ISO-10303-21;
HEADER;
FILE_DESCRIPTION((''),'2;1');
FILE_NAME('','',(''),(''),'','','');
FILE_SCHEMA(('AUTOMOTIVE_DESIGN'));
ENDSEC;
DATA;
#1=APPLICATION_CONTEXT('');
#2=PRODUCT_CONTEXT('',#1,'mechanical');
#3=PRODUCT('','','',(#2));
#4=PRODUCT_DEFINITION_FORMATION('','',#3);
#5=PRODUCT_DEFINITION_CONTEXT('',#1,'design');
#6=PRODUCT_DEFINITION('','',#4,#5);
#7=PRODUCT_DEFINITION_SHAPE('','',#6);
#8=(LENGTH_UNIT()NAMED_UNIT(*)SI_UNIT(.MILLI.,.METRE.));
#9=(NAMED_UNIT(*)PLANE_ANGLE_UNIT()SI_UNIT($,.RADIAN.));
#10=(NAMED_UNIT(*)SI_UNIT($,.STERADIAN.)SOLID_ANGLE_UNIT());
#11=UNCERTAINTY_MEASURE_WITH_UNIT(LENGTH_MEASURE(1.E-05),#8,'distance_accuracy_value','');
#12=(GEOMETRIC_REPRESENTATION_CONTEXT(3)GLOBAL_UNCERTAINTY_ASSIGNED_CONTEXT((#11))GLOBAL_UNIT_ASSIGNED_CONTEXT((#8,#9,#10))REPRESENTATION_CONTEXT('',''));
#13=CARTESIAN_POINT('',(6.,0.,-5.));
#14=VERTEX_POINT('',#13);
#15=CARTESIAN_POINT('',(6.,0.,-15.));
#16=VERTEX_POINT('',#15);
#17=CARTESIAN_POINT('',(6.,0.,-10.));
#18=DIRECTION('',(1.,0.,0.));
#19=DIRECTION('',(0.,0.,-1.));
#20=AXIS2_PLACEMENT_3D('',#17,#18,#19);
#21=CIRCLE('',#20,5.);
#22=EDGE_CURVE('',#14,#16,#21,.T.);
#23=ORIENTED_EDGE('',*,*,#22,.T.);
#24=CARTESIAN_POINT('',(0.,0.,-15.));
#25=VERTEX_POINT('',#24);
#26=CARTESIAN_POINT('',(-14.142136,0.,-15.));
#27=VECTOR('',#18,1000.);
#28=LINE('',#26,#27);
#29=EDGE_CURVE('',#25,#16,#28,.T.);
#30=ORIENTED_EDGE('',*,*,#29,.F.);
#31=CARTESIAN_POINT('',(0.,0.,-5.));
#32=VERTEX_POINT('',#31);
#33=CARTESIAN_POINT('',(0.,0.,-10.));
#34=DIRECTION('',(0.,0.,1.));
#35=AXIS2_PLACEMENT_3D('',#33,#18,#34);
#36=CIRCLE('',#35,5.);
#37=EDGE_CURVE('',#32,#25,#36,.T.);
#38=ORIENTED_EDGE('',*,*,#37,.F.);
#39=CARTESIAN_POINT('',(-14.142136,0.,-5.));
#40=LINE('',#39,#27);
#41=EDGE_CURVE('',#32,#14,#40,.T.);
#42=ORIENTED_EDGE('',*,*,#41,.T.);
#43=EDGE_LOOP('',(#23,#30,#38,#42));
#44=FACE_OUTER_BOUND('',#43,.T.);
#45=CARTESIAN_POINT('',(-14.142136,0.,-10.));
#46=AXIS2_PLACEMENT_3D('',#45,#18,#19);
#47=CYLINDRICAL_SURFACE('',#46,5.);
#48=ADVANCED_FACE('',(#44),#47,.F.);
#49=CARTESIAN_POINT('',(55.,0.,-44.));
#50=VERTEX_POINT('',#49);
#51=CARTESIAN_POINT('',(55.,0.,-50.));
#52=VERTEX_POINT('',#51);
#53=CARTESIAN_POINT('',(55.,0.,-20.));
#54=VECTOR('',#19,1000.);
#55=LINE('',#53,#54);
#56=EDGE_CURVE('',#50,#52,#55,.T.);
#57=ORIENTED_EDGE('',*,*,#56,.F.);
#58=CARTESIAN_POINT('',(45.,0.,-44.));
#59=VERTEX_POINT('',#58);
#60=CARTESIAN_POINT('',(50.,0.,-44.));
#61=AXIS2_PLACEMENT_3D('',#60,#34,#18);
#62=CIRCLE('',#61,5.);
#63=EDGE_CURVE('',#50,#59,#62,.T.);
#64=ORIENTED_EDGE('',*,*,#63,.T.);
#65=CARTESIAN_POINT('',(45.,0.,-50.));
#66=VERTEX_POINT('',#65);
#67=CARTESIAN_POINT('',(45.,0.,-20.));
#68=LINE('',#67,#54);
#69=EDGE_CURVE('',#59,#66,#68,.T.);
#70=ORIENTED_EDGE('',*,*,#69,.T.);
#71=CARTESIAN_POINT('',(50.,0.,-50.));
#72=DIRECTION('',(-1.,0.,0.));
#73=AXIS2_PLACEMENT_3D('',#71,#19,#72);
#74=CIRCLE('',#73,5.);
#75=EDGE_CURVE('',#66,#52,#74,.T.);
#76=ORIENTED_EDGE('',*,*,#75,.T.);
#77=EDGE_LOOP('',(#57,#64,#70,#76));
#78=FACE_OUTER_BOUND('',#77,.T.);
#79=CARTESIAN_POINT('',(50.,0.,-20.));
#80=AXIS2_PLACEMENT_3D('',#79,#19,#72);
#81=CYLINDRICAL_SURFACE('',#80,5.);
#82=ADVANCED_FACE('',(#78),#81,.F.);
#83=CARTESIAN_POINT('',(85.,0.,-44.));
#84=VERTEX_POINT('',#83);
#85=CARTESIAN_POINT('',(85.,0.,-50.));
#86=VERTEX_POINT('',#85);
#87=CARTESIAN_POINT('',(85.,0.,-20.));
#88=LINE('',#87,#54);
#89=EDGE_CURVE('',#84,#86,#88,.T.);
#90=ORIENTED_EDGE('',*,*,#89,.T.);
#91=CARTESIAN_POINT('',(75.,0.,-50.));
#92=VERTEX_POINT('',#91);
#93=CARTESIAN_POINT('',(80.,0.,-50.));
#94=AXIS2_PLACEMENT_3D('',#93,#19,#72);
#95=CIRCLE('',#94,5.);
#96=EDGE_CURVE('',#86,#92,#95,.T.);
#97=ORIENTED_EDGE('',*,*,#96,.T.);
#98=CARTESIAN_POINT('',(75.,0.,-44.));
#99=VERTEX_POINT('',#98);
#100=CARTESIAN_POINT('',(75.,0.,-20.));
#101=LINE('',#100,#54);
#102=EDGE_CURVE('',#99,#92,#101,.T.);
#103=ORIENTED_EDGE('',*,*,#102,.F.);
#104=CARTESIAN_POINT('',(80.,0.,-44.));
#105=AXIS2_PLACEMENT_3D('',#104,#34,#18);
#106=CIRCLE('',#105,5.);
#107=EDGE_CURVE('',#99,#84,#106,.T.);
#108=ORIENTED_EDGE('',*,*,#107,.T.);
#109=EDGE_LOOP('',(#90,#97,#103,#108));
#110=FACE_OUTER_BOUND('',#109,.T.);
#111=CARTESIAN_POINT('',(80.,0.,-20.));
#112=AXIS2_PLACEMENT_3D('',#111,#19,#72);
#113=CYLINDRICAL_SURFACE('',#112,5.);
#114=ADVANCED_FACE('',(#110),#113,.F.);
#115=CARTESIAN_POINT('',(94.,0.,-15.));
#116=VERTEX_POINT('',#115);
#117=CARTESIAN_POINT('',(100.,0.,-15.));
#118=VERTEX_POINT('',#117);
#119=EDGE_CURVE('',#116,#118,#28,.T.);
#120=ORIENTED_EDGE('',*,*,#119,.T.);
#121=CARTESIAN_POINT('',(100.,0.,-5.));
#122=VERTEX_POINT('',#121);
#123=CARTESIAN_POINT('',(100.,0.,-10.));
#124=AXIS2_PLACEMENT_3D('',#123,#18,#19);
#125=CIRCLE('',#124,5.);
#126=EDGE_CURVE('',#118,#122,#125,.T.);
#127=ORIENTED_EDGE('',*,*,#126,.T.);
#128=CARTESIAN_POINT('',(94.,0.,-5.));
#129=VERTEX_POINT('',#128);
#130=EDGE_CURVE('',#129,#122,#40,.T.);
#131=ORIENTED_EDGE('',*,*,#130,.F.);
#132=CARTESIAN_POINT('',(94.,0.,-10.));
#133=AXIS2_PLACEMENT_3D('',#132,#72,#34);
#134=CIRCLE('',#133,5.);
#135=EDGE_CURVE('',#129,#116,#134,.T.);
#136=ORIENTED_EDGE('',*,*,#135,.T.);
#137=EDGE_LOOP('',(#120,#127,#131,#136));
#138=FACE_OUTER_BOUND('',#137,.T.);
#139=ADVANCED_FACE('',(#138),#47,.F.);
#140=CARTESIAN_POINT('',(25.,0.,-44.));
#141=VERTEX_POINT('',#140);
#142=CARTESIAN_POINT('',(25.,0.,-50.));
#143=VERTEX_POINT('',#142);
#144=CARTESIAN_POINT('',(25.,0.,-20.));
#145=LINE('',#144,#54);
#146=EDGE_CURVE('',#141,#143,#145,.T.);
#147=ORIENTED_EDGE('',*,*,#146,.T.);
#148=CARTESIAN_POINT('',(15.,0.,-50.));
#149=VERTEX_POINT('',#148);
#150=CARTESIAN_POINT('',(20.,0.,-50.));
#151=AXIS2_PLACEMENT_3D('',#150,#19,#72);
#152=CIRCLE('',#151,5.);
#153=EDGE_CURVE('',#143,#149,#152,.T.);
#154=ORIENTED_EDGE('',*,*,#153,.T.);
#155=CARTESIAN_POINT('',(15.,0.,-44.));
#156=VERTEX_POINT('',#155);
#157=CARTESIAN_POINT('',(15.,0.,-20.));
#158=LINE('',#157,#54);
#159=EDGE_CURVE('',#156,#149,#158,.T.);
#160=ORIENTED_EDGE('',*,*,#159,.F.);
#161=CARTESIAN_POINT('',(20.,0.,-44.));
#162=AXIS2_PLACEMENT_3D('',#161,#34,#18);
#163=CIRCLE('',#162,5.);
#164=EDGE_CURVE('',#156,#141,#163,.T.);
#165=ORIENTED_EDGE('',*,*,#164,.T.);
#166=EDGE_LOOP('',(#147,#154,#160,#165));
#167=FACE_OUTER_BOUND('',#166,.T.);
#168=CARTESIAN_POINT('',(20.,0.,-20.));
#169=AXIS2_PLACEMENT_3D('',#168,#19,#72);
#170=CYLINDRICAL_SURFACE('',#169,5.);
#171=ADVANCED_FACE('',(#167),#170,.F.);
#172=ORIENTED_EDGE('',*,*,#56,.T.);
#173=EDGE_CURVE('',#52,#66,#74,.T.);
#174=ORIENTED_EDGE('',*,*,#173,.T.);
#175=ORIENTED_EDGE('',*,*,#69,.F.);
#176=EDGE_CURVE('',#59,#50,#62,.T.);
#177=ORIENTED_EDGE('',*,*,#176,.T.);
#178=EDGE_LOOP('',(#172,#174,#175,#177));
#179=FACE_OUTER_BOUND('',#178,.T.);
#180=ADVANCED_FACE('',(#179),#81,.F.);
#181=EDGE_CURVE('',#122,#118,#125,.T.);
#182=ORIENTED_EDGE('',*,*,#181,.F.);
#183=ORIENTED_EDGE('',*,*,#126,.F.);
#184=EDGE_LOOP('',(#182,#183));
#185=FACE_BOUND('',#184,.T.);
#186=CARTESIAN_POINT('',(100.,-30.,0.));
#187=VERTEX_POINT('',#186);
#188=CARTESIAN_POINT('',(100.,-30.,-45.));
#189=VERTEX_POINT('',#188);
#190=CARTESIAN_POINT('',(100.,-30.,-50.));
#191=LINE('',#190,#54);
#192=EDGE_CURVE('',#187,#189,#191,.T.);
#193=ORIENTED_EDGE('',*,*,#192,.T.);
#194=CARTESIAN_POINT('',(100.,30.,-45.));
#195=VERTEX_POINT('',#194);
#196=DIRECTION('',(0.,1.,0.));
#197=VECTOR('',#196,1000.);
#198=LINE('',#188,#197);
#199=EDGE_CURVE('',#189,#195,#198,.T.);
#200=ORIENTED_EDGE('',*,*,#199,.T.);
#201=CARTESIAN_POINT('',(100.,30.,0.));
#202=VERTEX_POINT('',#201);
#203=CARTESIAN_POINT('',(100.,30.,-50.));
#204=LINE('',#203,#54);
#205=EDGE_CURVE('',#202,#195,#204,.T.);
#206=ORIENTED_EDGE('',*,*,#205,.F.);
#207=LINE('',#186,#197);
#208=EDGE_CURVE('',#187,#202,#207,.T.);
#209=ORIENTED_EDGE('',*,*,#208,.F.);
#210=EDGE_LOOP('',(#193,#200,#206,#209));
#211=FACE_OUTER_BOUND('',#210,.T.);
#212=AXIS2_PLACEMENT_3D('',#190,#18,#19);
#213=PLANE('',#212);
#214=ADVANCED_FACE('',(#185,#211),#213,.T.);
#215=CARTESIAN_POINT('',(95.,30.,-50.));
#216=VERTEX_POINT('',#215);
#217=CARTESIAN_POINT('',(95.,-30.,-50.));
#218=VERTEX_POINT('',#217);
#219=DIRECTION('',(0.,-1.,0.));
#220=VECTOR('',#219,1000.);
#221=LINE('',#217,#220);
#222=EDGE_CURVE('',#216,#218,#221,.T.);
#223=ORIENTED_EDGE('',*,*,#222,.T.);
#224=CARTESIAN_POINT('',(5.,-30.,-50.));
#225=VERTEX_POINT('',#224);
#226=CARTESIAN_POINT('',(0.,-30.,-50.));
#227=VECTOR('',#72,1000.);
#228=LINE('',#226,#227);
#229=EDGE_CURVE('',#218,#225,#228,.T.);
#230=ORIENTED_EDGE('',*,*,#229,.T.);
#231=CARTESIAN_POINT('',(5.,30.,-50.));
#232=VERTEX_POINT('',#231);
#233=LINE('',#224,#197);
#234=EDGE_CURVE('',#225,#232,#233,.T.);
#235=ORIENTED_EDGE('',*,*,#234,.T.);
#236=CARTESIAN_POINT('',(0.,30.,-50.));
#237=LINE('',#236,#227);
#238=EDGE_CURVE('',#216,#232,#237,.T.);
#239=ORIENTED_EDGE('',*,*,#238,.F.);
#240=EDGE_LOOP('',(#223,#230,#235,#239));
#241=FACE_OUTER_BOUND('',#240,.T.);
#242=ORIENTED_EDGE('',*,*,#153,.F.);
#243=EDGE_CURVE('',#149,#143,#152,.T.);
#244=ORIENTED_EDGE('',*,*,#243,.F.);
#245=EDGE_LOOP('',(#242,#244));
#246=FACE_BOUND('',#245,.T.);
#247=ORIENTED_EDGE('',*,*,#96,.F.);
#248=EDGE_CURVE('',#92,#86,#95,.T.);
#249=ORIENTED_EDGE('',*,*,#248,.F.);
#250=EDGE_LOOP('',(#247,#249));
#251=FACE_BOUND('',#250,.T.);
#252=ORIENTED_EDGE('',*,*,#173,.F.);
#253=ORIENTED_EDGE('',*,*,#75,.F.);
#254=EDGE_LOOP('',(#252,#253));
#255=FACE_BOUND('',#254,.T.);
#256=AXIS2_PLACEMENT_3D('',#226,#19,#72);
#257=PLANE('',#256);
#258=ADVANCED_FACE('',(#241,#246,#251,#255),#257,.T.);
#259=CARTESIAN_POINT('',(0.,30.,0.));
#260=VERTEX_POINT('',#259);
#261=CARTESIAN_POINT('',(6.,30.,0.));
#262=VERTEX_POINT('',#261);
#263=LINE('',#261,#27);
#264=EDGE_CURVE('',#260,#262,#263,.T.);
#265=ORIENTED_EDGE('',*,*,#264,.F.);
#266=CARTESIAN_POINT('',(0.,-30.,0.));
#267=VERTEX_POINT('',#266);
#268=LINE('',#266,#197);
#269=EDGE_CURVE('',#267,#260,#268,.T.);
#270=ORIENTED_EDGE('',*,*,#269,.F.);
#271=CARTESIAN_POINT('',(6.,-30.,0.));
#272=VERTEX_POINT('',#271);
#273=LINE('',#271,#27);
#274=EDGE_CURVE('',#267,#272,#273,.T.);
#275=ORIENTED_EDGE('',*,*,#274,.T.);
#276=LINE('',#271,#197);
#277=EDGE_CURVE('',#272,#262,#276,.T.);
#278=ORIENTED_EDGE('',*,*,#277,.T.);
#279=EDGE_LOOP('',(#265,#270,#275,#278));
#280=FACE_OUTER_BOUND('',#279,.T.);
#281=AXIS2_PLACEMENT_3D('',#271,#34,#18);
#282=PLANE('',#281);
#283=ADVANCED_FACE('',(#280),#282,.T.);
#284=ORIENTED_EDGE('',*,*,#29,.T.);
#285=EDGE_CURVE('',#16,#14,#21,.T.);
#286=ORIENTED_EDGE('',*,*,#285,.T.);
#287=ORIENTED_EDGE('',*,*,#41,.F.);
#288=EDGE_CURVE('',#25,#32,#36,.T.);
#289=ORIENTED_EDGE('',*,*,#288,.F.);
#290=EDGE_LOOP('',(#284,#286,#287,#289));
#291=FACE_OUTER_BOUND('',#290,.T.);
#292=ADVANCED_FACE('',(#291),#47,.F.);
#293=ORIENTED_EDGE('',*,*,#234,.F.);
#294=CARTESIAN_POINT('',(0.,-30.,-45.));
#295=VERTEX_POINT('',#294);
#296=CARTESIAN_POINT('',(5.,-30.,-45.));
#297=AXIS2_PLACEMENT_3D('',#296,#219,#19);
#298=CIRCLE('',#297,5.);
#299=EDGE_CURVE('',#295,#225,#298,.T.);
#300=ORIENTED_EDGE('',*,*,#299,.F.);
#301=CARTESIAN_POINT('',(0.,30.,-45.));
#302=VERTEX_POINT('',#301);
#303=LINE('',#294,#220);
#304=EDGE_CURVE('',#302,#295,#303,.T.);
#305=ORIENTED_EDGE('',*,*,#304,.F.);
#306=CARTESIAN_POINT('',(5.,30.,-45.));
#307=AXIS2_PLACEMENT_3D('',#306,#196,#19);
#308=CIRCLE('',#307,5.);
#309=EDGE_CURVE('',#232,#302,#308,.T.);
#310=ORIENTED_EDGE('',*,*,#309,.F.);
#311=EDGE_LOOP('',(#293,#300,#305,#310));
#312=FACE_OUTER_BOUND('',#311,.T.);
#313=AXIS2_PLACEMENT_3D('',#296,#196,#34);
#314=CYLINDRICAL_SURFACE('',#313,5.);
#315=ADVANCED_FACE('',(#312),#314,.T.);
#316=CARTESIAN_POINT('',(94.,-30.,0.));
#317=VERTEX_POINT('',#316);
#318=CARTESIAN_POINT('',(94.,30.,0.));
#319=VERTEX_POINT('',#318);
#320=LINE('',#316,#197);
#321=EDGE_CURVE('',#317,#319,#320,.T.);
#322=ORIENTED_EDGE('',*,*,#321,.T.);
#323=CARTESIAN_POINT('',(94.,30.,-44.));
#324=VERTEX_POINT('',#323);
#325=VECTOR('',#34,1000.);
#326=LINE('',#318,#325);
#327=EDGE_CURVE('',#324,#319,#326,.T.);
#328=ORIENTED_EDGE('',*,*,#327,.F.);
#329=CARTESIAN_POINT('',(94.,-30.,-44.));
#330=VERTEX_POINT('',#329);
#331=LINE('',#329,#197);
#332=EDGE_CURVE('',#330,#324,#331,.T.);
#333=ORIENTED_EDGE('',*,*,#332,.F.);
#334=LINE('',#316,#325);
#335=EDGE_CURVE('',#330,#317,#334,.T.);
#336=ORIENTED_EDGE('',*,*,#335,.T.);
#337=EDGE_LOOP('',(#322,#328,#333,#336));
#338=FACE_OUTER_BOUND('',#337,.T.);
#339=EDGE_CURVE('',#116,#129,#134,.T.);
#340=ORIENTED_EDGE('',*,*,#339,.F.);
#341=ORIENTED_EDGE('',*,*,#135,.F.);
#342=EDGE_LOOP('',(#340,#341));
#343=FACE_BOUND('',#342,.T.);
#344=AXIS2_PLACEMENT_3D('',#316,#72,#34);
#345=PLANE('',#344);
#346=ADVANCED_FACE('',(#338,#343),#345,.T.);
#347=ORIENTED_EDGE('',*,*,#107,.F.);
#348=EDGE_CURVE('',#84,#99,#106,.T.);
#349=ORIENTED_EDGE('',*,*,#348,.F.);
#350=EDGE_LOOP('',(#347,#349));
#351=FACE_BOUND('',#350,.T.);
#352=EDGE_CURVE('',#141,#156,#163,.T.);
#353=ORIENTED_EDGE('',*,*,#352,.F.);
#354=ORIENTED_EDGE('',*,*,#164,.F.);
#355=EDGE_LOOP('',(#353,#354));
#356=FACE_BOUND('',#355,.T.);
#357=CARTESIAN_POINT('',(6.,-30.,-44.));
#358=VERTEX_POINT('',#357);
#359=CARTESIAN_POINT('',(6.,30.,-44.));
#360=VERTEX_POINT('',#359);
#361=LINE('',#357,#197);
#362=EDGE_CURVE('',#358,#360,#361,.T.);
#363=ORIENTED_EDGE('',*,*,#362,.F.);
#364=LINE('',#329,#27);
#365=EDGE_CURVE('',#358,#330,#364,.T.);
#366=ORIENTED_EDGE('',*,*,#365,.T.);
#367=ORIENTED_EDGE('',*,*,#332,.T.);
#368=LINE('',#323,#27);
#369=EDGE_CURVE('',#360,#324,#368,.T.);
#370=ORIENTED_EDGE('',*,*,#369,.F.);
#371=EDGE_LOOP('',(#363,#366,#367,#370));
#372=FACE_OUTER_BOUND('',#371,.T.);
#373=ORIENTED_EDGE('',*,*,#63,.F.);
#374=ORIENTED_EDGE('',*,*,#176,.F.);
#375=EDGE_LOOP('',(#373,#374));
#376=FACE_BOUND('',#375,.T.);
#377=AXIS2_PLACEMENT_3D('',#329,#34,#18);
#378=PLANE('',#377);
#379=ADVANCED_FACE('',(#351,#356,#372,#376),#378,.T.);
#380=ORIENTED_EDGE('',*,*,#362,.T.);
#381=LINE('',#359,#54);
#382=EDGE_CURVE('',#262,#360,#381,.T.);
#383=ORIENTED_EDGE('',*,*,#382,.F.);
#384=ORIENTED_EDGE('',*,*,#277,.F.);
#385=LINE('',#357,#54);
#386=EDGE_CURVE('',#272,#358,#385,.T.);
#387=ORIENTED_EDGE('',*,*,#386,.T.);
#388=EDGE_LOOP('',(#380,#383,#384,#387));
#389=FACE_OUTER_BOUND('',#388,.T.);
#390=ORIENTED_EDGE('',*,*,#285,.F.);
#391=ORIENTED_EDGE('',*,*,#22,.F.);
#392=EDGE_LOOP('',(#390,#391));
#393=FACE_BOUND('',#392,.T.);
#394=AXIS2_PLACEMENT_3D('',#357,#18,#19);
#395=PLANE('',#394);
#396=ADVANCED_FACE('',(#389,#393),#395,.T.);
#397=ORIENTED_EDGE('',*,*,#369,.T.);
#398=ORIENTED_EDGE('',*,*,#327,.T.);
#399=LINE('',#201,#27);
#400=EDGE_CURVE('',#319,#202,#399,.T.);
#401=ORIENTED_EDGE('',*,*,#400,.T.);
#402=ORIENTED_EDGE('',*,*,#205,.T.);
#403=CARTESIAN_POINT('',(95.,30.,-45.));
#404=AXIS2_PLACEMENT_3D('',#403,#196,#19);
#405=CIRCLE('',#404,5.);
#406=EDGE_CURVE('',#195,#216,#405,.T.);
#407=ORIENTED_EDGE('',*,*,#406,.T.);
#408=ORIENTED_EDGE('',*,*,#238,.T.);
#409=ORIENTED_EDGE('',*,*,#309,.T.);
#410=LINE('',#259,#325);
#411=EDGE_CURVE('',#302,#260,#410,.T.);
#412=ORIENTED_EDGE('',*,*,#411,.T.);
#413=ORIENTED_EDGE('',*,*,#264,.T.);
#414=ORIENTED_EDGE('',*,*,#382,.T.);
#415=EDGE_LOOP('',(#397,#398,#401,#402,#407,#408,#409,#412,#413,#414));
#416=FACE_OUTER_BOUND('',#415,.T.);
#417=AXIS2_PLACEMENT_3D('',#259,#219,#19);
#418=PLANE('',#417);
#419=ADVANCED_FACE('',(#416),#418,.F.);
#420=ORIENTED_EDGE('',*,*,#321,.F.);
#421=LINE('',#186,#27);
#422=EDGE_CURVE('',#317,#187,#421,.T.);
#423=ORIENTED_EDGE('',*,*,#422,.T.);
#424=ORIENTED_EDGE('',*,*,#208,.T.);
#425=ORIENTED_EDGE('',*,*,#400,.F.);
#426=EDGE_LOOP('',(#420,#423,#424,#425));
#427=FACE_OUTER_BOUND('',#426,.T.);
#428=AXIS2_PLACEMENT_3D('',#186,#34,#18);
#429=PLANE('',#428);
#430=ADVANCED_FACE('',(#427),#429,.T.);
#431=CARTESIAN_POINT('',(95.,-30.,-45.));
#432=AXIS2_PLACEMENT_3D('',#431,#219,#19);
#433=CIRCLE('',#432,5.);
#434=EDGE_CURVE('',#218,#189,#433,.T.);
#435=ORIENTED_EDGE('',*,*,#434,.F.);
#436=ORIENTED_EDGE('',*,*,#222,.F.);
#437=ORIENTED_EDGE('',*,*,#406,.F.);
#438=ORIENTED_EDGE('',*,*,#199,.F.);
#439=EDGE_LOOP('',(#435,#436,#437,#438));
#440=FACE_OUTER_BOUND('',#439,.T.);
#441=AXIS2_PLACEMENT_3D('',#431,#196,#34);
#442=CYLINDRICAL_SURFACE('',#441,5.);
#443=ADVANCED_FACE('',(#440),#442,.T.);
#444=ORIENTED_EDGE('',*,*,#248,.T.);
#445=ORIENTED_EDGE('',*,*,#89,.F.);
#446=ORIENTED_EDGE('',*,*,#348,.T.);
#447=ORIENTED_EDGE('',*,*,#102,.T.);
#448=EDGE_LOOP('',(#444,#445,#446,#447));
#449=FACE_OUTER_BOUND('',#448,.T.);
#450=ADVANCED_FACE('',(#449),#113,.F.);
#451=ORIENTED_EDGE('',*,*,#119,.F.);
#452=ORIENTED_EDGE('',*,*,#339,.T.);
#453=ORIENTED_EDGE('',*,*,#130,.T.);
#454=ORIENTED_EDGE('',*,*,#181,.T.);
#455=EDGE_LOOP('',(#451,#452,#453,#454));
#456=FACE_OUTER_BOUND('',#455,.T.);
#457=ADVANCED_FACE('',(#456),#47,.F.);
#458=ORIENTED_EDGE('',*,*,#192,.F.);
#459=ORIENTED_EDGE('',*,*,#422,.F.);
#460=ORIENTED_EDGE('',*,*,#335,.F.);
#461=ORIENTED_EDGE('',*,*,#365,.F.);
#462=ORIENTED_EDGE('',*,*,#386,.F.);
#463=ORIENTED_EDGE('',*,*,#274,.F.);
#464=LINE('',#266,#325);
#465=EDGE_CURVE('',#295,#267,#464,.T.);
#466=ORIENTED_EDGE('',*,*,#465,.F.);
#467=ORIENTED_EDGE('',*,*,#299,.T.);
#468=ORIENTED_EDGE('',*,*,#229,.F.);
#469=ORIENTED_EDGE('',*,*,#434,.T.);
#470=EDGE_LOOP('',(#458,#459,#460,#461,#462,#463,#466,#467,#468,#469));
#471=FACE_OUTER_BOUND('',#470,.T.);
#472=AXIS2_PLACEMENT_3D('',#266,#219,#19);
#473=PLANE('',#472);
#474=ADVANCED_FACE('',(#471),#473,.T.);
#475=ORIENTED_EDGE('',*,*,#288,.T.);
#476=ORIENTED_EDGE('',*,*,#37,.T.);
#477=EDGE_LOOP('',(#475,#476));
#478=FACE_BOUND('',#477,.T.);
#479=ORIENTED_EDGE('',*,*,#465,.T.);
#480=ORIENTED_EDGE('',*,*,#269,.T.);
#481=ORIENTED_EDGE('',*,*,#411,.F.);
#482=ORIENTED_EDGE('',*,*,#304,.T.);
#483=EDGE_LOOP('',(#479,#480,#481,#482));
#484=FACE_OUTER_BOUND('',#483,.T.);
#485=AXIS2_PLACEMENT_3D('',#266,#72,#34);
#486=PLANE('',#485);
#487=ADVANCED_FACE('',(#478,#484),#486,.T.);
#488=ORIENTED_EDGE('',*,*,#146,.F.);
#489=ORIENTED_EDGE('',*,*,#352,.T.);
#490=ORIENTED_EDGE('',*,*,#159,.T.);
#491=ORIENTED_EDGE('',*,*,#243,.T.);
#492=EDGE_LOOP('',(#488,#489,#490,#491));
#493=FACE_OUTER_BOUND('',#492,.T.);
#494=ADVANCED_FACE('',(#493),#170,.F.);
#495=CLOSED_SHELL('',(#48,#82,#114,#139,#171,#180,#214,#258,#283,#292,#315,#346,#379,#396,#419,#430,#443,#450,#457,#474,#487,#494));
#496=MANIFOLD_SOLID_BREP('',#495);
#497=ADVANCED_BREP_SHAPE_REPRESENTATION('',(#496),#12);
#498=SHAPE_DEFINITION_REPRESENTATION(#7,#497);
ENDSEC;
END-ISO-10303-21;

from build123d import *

# Parameters (mm, degrees)
CHANNEL_BODY_DEPTH      = 30
FLANGE_HOLES_SKETCH_R   = 5
FLANGE_HOLES_DEPTH      = 30
BACK_WALL_HOLES_REACH   = 117.758
BACK_WALL_HOLE_SKETCH_R = 5
CORNER_FILLETS_R5_R     = 5


with BuildPart() as part:
    # Channel Profile Sketch → Channel Body (new, symmetric)
    with BuildSketch(Plane(origin=(0, 0, 0), x_dir=(1, 0, 0), z_dir=(0, 1, 0))):
        Polygon((0, 0), (0, 50), (100, 50), (100, 0), (94, 0), (94, 44), (6, 44), (6, 0), align=None)
    extrude(amount=CHANNEL_BODY_DEPTH, both=True)

    # Flange Holes Sketch → Flange Holes (cut, symmetric)
    with BuildSketch(Plane(origin=(0, 0, -50), x_dir=(-1, 0, 0), z_dir=(0, 0, -1))):
        with Locations((-50, 0)):
            Circle(FLANGE_HOLES_SKETCH_R)
        with Locations((-20, 0)):
            Circle(FLANGE_HOLES_SKETCH_R)
        with Locations((-80, 0)):
            Circle(FLANGE_HOLES_SKETCH_R)
    extrude(amount=FLANGE_HOLES_DEPTH, both=True, mode=Mode.SUBTRACT)

    # Back Wall Holes: up to this face of the body (flat: up to its plane)
    back_wall_holes_end = Plane(part.part.faces().sort_by_distance((0, 0, -25))[0])
    # Back Wall Hole Sketch → Back Wall Holes (cut, up to the picked face)
    with BuildSketch(Plane(origin=(100, 0, 0), x_dir=(0, 0, -1), z_dir=(1, 0, 0)), mode=Mode.PRIVATE) as back_wall_holes_sk1:
        with Locations((10, 0)):
            Circle(BACK_WALL_HOLE_SKETCH_R)
    back_wall_holes_tool1 = split(extrude(back_wall_holes_sk1.sketch, amount=-BACK_WALL_HOLES_REACH, mode=Mode.PRIVATE), bisect_by=back_wall_holes_end, keep=Keep.BOTH, mode=Mode.PRIVATE)
    add(back_wall_holes_tool1.solids().sort_by(Axis((100, 0, -10), (-1, 0, 0)))[0], mode=Mode.SUBTRACT)

    # Corner Fillets R5
    corner_fillets_r5_edges = [part.edges().sort_by_distance(p)[0] for p in [
        (0, 0, -50),
        (100, 0, -50),
    ]]
    fillet(corner_fillets_r5_edges, radius=CORNER_FILLETS_R5_R)


solid = part.part
